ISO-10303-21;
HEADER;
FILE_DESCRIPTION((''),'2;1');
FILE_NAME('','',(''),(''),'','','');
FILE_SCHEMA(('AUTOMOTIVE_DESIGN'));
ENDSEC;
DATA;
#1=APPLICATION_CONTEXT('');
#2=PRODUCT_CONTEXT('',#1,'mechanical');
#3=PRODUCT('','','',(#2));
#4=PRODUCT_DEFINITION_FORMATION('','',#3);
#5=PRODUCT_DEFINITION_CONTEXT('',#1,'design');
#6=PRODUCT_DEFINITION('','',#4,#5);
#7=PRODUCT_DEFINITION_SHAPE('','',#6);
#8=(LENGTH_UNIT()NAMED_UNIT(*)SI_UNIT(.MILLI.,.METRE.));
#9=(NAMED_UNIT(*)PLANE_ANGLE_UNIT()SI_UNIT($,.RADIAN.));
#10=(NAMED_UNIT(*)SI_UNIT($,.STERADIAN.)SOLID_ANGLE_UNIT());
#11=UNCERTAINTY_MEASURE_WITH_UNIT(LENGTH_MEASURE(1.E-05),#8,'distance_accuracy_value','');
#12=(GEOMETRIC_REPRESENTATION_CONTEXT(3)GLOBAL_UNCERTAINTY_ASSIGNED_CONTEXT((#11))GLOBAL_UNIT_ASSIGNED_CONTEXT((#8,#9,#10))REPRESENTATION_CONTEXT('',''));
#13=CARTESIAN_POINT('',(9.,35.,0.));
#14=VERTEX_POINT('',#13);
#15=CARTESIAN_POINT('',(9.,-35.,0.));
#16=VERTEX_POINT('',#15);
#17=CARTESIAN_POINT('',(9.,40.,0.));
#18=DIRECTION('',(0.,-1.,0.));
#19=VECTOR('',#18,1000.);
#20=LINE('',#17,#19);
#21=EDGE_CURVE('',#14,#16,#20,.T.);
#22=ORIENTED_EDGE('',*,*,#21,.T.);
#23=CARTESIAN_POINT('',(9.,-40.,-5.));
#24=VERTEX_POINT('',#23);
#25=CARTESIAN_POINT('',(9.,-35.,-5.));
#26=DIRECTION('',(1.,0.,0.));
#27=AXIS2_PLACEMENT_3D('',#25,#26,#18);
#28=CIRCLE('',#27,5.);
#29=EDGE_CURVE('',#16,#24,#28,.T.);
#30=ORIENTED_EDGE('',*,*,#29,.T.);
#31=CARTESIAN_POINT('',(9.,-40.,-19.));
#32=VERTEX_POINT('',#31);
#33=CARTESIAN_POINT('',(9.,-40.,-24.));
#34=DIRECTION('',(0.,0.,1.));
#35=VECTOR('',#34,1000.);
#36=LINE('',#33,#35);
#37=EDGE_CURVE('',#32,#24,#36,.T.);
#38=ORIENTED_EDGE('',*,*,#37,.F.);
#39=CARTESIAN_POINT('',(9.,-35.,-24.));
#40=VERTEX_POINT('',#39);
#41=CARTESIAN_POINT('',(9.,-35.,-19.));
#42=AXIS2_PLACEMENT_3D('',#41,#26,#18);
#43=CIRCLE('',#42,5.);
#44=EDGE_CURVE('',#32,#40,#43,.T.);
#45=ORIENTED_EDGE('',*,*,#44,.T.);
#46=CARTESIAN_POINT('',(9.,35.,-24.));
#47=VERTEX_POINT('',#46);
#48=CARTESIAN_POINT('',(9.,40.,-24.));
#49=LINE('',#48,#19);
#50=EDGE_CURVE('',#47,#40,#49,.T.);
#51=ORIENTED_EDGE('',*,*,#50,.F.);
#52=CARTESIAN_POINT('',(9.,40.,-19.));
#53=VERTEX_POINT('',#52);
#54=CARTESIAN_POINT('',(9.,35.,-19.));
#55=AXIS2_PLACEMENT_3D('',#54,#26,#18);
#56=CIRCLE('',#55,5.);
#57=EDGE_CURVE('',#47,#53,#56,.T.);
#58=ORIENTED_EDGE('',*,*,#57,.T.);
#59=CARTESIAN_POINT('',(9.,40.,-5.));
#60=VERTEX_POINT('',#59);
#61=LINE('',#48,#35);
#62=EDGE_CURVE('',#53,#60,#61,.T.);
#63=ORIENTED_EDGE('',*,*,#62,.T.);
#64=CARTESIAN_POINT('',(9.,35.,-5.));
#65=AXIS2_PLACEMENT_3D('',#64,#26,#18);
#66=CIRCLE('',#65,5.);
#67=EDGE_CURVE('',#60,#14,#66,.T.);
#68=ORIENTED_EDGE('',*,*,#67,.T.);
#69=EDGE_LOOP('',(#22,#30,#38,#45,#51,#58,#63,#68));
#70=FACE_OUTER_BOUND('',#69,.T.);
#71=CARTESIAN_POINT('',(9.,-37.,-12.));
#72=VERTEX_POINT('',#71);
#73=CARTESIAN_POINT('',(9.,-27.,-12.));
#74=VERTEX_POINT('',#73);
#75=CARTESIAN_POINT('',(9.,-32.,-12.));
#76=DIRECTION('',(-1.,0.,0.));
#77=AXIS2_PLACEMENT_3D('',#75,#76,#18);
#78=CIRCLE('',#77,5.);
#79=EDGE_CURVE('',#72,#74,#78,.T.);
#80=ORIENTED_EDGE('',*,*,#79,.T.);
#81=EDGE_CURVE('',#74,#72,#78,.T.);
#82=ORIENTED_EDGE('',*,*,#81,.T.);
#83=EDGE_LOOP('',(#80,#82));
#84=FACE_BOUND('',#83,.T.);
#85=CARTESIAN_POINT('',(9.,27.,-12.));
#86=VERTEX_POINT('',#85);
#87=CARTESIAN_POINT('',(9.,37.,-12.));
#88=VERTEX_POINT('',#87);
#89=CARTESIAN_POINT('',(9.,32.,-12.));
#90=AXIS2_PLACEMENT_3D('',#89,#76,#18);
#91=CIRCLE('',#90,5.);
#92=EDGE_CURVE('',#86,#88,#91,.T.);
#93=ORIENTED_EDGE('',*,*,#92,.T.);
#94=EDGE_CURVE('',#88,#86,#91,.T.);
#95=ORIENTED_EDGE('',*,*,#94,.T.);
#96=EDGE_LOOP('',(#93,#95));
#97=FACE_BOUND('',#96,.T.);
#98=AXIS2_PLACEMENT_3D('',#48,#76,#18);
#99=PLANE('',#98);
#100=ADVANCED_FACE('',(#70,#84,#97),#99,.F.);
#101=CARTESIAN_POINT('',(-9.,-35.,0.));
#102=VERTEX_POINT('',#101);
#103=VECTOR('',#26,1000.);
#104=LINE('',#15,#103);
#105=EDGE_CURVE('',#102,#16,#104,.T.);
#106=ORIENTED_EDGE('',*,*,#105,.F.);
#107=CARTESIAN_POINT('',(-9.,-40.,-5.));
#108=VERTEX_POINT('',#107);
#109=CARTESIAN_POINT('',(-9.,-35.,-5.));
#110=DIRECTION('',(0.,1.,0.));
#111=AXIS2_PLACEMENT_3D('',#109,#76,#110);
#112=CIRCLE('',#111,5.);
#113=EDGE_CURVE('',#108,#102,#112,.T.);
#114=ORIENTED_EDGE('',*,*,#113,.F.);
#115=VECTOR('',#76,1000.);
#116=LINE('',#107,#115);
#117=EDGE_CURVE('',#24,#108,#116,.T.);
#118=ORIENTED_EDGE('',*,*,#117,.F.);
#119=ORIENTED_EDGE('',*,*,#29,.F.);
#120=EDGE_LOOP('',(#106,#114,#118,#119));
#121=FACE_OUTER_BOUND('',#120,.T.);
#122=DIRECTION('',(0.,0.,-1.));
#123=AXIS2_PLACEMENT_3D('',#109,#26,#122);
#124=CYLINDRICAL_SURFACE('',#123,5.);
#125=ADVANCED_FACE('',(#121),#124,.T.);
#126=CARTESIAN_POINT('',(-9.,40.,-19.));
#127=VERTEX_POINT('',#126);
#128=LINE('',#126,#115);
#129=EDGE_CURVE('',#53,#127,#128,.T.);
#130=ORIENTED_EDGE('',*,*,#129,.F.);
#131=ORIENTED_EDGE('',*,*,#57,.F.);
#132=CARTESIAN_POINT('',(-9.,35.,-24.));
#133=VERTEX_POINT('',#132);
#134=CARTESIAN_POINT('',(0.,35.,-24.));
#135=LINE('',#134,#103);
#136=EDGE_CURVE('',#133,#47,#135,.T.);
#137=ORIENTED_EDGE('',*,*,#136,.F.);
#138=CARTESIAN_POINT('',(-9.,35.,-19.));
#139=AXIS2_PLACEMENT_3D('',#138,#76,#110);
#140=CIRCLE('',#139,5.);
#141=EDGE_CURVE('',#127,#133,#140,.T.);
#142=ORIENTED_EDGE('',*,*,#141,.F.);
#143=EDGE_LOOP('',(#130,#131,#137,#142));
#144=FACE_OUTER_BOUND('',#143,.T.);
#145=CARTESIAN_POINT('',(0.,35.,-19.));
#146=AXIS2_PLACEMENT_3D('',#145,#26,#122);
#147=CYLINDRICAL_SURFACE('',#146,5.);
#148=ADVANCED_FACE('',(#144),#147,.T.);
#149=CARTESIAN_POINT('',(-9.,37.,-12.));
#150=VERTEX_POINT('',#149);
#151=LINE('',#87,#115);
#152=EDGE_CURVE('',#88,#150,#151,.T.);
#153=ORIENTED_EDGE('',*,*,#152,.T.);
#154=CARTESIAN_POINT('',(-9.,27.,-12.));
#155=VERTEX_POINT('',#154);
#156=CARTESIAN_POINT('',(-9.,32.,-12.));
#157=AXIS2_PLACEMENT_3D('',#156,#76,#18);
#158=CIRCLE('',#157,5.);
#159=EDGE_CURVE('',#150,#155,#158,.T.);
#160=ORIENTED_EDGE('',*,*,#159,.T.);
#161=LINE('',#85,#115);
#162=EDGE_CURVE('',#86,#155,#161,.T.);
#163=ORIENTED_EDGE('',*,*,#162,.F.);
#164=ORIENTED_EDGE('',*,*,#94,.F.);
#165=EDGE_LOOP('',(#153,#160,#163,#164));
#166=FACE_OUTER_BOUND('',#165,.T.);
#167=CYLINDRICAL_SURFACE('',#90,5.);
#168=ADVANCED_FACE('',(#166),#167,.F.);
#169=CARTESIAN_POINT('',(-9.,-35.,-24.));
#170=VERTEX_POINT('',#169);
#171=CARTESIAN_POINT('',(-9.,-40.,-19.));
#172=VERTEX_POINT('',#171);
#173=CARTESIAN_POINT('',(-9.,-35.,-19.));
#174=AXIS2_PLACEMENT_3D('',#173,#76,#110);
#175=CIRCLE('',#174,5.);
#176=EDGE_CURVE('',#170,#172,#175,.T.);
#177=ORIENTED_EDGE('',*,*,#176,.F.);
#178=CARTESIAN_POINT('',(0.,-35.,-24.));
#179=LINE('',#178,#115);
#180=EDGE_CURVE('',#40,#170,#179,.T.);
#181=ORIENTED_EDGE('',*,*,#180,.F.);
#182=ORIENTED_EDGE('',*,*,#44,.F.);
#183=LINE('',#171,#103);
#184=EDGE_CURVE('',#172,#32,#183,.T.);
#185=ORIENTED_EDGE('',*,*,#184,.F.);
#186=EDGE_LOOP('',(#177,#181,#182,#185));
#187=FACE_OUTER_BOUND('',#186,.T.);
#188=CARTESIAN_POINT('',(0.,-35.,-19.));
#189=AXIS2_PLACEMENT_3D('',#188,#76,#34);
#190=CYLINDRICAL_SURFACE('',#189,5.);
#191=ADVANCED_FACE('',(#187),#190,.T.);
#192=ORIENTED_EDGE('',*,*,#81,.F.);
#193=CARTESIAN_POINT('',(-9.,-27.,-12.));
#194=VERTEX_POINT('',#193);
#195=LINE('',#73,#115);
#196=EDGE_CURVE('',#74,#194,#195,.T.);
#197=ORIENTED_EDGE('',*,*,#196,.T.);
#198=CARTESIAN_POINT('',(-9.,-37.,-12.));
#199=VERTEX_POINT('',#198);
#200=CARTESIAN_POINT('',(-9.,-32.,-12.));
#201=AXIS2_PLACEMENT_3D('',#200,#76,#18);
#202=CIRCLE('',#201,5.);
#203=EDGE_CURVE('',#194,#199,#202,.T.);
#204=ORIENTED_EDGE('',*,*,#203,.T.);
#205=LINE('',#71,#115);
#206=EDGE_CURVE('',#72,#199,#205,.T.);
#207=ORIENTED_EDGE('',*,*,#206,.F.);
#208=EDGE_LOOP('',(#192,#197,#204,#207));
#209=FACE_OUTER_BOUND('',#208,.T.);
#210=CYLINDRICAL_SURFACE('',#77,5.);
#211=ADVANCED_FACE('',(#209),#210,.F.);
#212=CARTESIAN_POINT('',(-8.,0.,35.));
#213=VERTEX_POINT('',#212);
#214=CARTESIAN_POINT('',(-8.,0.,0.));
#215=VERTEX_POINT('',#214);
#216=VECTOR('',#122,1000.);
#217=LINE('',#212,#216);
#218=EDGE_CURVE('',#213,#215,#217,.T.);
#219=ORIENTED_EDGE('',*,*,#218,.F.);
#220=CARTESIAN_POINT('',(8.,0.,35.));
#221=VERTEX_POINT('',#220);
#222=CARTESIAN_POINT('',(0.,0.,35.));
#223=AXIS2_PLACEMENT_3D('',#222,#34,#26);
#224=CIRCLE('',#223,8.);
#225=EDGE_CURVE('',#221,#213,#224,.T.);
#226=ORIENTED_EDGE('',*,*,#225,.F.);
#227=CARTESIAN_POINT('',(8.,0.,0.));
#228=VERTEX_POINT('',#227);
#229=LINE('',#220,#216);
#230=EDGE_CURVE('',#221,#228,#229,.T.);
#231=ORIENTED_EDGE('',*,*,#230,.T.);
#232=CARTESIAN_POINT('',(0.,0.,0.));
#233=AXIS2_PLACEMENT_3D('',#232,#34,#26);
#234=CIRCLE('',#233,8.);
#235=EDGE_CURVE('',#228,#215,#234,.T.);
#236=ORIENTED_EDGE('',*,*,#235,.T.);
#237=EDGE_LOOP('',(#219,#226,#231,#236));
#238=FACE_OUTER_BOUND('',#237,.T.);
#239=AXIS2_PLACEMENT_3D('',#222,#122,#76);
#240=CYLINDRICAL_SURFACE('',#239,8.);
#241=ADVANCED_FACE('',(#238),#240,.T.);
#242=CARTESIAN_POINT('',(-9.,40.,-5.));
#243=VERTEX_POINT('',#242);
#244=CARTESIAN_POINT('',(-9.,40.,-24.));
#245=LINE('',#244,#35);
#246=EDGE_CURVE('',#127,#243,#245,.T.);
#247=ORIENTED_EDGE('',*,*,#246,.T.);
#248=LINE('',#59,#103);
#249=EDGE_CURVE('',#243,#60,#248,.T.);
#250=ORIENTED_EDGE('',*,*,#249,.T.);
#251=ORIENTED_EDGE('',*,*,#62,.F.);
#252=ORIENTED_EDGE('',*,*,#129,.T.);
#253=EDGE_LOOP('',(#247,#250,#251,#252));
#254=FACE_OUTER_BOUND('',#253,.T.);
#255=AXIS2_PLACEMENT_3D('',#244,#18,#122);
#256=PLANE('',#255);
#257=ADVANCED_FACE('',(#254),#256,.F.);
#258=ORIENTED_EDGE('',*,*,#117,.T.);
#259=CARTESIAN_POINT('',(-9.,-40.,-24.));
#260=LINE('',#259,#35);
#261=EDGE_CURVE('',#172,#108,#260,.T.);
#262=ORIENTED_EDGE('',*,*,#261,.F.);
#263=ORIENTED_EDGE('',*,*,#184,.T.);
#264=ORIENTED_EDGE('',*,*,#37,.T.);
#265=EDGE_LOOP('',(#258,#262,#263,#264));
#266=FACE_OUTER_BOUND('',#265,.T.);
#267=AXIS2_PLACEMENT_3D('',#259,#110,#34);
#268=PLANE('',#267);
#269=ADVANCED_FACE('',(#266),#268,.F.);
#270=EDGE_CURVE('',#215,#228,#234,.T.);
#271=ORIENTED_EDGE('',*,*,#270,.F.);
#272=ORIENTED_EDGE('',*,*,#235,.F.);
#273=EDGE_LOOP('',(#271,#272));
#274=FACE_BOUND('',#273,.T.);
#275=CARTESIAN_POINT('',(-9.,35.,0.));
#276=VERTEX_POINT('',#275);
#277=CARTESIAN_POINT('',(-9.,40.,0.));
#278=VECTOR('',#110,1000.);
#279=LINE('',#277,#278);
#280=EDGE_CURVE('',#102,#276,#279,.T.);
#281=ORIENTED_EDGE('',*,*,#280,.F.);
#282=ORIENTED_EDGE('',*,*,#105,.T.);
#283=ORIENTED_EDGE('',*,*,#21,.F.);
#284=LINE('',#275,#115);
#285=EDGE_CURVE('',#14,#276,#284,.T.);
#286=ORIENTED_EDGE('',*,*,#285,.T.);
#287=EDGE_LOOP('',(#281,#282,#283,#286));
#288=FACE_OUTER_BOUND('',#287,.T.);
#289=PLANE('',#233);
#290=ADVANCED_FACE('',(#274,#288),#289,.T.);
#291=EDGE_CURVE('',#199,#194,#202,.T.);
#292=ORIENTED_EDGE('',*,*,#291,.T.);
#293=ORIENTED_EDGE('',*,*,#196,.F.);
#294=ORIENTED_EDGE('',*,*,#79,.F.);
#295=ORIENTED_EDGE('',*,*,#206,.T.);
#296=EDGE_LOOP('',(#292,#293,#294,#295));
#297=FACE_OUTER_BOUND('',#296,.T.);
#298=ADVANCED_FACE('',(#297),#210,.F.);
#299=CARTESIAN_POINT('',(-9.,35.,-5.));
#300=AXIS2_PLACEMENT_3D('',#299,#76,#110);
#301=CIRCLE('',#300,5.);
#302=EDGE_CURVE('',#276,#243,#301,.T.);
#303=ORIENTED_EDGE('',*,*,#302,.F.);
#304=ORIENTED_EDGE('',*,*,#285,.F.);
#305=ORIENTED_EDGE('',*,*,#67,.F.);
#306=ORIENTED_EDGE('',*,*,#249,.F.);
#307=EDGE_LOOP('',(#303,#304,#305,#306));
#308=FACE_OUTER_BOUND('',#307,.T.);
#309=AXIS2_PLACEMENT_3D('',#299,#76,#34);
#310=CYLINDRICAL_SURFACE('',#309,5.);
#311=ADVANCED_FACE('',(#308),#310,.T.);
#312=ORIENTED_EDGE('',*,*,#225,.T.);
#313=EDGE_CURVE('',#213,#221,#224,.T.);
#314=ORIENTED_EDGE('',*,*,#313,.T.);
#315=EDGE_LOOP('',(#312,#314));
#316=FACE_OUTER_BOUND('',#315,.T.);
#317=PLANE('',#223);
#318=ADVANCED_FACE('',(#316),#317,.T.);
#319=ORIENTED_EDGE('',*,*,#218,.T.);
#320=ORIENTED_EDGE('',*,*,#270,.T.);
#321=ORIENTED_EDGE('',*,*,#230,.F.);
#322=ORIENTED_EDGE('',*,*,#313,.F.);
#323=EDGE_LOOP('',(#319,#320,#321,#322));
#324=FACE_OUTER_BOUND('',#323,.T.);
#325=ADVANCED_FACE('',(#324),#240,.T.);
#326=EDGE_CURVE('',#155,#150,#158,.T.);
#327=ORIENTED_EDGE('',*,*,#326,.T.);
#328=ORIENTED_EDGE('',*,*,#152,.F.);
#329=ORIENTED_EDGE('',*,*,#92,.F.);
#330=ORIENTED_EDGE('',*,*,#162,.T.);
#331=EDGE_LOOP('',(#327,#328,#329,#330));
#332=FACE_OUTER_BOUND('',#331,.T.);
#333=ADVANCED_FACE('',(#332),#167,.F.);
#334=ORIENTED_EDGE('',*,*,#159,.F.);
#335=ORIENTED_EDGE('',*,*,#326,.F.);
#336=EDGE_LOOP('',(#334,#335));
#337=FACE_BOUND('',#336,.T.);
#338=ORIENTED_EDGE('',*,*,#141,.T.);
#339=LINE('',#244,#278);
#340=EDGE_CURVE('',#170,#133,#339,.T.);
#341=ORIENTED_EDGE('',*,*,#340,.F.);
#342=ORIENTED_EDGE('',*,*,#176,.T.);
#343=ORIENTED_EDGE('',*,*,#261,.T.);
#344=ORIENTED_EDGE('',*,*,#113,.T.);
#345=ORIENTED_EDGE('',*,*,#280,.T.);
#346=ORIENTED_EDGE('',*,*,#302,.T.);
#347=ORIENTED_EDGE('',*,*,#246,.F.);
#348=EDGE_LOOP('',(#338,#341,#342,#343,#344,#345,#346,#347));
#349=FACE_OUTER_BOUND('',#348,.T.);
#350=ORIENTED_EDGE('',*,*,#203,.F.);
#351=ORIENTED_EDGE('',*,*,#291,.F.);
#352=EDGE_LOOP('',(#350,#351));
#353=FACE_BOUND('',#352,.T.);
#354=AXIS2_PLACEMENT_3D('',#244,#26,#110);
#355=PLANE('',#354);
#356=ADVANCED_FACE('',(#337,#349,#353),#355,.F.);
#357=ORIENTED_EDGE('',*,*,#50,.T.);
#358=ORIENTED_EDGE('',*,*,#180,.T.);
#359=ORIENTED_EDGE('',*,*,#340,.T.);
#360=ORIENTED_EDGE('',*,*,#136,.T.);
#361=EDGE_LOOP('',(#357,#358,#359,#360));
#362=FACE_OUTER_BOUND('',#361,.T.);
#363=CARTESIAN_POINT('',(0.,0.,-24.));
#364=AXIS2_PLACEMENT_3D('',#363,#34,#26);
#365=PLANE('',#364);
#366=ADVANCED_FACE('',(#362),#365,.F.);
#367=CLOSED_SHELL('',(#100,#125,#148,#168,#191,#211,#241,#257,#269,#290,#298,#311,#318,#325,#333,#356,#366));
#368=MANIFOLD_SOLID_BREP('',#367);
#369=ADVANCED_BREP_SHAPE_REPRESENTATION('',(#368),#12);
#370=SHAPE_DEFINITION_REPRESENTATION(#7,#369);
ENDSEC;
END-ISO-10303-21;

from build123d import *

# Parameters (mm, degrees)
SKETCH1_R           = 8
BOSS_EXTRUDE1_DEPTH = 35
SKETCH2_W           = 18
SKETCH2_H           = 80
BOSS_EXTRUDE2_DEPTH = 24
FILLET1_R           = 5
SKETCH4_R           = 5
CUT_EXTRUDE1_DEPTH  = 57.115951386


with BuildPart() as part:
    # Sketch1 → Boss-Extrude1 (new body)
    with BuildSketch(Plane.XY):
        Circle(SKETCH1_R)
    extrude(amount=BOSS_EXTRUDE1_DEPTH)

    # Sketch2 → Boss-Extrude2 (add)
    with BuildSketch(Plane(origin=(0, 0, 0), x_dir=(-1, 0, 0), z_dir=(0, 0, -1))):
        Rectangle(SKETCH2_W, SKETCH2_H)
    extrude(amount=BOSS_EXTRUDE2_DEPTH)

    # Fillet1
    fillet1_edges = [part.edges().sort_by_distance(p)[0] for p in [
        (0, -40, 0),
        (0, 40, 0),
        (0, -40, -24),
        (0, 40, -24),
    ]]
    fillet(fillet1_edges, radius=FILLET1_R)

    # Sketch4 → Cut-Extrude1 (cut, through all)
    with BuildSketch(Plane.ZY.offset(9)):
        with Locations(Location((-12, -32, 0), (0, 0, 270))):
            Circle(SKETCH4_R)
        with Locations(Location((-12, 32, 0), (0, 0, 270))):
            Circle(SKETCH4_R)
    extrude(amount=-CUT_EXTRUDE1_DEPTH, mode=Mode.SUBTRACT)


solid = part.part
